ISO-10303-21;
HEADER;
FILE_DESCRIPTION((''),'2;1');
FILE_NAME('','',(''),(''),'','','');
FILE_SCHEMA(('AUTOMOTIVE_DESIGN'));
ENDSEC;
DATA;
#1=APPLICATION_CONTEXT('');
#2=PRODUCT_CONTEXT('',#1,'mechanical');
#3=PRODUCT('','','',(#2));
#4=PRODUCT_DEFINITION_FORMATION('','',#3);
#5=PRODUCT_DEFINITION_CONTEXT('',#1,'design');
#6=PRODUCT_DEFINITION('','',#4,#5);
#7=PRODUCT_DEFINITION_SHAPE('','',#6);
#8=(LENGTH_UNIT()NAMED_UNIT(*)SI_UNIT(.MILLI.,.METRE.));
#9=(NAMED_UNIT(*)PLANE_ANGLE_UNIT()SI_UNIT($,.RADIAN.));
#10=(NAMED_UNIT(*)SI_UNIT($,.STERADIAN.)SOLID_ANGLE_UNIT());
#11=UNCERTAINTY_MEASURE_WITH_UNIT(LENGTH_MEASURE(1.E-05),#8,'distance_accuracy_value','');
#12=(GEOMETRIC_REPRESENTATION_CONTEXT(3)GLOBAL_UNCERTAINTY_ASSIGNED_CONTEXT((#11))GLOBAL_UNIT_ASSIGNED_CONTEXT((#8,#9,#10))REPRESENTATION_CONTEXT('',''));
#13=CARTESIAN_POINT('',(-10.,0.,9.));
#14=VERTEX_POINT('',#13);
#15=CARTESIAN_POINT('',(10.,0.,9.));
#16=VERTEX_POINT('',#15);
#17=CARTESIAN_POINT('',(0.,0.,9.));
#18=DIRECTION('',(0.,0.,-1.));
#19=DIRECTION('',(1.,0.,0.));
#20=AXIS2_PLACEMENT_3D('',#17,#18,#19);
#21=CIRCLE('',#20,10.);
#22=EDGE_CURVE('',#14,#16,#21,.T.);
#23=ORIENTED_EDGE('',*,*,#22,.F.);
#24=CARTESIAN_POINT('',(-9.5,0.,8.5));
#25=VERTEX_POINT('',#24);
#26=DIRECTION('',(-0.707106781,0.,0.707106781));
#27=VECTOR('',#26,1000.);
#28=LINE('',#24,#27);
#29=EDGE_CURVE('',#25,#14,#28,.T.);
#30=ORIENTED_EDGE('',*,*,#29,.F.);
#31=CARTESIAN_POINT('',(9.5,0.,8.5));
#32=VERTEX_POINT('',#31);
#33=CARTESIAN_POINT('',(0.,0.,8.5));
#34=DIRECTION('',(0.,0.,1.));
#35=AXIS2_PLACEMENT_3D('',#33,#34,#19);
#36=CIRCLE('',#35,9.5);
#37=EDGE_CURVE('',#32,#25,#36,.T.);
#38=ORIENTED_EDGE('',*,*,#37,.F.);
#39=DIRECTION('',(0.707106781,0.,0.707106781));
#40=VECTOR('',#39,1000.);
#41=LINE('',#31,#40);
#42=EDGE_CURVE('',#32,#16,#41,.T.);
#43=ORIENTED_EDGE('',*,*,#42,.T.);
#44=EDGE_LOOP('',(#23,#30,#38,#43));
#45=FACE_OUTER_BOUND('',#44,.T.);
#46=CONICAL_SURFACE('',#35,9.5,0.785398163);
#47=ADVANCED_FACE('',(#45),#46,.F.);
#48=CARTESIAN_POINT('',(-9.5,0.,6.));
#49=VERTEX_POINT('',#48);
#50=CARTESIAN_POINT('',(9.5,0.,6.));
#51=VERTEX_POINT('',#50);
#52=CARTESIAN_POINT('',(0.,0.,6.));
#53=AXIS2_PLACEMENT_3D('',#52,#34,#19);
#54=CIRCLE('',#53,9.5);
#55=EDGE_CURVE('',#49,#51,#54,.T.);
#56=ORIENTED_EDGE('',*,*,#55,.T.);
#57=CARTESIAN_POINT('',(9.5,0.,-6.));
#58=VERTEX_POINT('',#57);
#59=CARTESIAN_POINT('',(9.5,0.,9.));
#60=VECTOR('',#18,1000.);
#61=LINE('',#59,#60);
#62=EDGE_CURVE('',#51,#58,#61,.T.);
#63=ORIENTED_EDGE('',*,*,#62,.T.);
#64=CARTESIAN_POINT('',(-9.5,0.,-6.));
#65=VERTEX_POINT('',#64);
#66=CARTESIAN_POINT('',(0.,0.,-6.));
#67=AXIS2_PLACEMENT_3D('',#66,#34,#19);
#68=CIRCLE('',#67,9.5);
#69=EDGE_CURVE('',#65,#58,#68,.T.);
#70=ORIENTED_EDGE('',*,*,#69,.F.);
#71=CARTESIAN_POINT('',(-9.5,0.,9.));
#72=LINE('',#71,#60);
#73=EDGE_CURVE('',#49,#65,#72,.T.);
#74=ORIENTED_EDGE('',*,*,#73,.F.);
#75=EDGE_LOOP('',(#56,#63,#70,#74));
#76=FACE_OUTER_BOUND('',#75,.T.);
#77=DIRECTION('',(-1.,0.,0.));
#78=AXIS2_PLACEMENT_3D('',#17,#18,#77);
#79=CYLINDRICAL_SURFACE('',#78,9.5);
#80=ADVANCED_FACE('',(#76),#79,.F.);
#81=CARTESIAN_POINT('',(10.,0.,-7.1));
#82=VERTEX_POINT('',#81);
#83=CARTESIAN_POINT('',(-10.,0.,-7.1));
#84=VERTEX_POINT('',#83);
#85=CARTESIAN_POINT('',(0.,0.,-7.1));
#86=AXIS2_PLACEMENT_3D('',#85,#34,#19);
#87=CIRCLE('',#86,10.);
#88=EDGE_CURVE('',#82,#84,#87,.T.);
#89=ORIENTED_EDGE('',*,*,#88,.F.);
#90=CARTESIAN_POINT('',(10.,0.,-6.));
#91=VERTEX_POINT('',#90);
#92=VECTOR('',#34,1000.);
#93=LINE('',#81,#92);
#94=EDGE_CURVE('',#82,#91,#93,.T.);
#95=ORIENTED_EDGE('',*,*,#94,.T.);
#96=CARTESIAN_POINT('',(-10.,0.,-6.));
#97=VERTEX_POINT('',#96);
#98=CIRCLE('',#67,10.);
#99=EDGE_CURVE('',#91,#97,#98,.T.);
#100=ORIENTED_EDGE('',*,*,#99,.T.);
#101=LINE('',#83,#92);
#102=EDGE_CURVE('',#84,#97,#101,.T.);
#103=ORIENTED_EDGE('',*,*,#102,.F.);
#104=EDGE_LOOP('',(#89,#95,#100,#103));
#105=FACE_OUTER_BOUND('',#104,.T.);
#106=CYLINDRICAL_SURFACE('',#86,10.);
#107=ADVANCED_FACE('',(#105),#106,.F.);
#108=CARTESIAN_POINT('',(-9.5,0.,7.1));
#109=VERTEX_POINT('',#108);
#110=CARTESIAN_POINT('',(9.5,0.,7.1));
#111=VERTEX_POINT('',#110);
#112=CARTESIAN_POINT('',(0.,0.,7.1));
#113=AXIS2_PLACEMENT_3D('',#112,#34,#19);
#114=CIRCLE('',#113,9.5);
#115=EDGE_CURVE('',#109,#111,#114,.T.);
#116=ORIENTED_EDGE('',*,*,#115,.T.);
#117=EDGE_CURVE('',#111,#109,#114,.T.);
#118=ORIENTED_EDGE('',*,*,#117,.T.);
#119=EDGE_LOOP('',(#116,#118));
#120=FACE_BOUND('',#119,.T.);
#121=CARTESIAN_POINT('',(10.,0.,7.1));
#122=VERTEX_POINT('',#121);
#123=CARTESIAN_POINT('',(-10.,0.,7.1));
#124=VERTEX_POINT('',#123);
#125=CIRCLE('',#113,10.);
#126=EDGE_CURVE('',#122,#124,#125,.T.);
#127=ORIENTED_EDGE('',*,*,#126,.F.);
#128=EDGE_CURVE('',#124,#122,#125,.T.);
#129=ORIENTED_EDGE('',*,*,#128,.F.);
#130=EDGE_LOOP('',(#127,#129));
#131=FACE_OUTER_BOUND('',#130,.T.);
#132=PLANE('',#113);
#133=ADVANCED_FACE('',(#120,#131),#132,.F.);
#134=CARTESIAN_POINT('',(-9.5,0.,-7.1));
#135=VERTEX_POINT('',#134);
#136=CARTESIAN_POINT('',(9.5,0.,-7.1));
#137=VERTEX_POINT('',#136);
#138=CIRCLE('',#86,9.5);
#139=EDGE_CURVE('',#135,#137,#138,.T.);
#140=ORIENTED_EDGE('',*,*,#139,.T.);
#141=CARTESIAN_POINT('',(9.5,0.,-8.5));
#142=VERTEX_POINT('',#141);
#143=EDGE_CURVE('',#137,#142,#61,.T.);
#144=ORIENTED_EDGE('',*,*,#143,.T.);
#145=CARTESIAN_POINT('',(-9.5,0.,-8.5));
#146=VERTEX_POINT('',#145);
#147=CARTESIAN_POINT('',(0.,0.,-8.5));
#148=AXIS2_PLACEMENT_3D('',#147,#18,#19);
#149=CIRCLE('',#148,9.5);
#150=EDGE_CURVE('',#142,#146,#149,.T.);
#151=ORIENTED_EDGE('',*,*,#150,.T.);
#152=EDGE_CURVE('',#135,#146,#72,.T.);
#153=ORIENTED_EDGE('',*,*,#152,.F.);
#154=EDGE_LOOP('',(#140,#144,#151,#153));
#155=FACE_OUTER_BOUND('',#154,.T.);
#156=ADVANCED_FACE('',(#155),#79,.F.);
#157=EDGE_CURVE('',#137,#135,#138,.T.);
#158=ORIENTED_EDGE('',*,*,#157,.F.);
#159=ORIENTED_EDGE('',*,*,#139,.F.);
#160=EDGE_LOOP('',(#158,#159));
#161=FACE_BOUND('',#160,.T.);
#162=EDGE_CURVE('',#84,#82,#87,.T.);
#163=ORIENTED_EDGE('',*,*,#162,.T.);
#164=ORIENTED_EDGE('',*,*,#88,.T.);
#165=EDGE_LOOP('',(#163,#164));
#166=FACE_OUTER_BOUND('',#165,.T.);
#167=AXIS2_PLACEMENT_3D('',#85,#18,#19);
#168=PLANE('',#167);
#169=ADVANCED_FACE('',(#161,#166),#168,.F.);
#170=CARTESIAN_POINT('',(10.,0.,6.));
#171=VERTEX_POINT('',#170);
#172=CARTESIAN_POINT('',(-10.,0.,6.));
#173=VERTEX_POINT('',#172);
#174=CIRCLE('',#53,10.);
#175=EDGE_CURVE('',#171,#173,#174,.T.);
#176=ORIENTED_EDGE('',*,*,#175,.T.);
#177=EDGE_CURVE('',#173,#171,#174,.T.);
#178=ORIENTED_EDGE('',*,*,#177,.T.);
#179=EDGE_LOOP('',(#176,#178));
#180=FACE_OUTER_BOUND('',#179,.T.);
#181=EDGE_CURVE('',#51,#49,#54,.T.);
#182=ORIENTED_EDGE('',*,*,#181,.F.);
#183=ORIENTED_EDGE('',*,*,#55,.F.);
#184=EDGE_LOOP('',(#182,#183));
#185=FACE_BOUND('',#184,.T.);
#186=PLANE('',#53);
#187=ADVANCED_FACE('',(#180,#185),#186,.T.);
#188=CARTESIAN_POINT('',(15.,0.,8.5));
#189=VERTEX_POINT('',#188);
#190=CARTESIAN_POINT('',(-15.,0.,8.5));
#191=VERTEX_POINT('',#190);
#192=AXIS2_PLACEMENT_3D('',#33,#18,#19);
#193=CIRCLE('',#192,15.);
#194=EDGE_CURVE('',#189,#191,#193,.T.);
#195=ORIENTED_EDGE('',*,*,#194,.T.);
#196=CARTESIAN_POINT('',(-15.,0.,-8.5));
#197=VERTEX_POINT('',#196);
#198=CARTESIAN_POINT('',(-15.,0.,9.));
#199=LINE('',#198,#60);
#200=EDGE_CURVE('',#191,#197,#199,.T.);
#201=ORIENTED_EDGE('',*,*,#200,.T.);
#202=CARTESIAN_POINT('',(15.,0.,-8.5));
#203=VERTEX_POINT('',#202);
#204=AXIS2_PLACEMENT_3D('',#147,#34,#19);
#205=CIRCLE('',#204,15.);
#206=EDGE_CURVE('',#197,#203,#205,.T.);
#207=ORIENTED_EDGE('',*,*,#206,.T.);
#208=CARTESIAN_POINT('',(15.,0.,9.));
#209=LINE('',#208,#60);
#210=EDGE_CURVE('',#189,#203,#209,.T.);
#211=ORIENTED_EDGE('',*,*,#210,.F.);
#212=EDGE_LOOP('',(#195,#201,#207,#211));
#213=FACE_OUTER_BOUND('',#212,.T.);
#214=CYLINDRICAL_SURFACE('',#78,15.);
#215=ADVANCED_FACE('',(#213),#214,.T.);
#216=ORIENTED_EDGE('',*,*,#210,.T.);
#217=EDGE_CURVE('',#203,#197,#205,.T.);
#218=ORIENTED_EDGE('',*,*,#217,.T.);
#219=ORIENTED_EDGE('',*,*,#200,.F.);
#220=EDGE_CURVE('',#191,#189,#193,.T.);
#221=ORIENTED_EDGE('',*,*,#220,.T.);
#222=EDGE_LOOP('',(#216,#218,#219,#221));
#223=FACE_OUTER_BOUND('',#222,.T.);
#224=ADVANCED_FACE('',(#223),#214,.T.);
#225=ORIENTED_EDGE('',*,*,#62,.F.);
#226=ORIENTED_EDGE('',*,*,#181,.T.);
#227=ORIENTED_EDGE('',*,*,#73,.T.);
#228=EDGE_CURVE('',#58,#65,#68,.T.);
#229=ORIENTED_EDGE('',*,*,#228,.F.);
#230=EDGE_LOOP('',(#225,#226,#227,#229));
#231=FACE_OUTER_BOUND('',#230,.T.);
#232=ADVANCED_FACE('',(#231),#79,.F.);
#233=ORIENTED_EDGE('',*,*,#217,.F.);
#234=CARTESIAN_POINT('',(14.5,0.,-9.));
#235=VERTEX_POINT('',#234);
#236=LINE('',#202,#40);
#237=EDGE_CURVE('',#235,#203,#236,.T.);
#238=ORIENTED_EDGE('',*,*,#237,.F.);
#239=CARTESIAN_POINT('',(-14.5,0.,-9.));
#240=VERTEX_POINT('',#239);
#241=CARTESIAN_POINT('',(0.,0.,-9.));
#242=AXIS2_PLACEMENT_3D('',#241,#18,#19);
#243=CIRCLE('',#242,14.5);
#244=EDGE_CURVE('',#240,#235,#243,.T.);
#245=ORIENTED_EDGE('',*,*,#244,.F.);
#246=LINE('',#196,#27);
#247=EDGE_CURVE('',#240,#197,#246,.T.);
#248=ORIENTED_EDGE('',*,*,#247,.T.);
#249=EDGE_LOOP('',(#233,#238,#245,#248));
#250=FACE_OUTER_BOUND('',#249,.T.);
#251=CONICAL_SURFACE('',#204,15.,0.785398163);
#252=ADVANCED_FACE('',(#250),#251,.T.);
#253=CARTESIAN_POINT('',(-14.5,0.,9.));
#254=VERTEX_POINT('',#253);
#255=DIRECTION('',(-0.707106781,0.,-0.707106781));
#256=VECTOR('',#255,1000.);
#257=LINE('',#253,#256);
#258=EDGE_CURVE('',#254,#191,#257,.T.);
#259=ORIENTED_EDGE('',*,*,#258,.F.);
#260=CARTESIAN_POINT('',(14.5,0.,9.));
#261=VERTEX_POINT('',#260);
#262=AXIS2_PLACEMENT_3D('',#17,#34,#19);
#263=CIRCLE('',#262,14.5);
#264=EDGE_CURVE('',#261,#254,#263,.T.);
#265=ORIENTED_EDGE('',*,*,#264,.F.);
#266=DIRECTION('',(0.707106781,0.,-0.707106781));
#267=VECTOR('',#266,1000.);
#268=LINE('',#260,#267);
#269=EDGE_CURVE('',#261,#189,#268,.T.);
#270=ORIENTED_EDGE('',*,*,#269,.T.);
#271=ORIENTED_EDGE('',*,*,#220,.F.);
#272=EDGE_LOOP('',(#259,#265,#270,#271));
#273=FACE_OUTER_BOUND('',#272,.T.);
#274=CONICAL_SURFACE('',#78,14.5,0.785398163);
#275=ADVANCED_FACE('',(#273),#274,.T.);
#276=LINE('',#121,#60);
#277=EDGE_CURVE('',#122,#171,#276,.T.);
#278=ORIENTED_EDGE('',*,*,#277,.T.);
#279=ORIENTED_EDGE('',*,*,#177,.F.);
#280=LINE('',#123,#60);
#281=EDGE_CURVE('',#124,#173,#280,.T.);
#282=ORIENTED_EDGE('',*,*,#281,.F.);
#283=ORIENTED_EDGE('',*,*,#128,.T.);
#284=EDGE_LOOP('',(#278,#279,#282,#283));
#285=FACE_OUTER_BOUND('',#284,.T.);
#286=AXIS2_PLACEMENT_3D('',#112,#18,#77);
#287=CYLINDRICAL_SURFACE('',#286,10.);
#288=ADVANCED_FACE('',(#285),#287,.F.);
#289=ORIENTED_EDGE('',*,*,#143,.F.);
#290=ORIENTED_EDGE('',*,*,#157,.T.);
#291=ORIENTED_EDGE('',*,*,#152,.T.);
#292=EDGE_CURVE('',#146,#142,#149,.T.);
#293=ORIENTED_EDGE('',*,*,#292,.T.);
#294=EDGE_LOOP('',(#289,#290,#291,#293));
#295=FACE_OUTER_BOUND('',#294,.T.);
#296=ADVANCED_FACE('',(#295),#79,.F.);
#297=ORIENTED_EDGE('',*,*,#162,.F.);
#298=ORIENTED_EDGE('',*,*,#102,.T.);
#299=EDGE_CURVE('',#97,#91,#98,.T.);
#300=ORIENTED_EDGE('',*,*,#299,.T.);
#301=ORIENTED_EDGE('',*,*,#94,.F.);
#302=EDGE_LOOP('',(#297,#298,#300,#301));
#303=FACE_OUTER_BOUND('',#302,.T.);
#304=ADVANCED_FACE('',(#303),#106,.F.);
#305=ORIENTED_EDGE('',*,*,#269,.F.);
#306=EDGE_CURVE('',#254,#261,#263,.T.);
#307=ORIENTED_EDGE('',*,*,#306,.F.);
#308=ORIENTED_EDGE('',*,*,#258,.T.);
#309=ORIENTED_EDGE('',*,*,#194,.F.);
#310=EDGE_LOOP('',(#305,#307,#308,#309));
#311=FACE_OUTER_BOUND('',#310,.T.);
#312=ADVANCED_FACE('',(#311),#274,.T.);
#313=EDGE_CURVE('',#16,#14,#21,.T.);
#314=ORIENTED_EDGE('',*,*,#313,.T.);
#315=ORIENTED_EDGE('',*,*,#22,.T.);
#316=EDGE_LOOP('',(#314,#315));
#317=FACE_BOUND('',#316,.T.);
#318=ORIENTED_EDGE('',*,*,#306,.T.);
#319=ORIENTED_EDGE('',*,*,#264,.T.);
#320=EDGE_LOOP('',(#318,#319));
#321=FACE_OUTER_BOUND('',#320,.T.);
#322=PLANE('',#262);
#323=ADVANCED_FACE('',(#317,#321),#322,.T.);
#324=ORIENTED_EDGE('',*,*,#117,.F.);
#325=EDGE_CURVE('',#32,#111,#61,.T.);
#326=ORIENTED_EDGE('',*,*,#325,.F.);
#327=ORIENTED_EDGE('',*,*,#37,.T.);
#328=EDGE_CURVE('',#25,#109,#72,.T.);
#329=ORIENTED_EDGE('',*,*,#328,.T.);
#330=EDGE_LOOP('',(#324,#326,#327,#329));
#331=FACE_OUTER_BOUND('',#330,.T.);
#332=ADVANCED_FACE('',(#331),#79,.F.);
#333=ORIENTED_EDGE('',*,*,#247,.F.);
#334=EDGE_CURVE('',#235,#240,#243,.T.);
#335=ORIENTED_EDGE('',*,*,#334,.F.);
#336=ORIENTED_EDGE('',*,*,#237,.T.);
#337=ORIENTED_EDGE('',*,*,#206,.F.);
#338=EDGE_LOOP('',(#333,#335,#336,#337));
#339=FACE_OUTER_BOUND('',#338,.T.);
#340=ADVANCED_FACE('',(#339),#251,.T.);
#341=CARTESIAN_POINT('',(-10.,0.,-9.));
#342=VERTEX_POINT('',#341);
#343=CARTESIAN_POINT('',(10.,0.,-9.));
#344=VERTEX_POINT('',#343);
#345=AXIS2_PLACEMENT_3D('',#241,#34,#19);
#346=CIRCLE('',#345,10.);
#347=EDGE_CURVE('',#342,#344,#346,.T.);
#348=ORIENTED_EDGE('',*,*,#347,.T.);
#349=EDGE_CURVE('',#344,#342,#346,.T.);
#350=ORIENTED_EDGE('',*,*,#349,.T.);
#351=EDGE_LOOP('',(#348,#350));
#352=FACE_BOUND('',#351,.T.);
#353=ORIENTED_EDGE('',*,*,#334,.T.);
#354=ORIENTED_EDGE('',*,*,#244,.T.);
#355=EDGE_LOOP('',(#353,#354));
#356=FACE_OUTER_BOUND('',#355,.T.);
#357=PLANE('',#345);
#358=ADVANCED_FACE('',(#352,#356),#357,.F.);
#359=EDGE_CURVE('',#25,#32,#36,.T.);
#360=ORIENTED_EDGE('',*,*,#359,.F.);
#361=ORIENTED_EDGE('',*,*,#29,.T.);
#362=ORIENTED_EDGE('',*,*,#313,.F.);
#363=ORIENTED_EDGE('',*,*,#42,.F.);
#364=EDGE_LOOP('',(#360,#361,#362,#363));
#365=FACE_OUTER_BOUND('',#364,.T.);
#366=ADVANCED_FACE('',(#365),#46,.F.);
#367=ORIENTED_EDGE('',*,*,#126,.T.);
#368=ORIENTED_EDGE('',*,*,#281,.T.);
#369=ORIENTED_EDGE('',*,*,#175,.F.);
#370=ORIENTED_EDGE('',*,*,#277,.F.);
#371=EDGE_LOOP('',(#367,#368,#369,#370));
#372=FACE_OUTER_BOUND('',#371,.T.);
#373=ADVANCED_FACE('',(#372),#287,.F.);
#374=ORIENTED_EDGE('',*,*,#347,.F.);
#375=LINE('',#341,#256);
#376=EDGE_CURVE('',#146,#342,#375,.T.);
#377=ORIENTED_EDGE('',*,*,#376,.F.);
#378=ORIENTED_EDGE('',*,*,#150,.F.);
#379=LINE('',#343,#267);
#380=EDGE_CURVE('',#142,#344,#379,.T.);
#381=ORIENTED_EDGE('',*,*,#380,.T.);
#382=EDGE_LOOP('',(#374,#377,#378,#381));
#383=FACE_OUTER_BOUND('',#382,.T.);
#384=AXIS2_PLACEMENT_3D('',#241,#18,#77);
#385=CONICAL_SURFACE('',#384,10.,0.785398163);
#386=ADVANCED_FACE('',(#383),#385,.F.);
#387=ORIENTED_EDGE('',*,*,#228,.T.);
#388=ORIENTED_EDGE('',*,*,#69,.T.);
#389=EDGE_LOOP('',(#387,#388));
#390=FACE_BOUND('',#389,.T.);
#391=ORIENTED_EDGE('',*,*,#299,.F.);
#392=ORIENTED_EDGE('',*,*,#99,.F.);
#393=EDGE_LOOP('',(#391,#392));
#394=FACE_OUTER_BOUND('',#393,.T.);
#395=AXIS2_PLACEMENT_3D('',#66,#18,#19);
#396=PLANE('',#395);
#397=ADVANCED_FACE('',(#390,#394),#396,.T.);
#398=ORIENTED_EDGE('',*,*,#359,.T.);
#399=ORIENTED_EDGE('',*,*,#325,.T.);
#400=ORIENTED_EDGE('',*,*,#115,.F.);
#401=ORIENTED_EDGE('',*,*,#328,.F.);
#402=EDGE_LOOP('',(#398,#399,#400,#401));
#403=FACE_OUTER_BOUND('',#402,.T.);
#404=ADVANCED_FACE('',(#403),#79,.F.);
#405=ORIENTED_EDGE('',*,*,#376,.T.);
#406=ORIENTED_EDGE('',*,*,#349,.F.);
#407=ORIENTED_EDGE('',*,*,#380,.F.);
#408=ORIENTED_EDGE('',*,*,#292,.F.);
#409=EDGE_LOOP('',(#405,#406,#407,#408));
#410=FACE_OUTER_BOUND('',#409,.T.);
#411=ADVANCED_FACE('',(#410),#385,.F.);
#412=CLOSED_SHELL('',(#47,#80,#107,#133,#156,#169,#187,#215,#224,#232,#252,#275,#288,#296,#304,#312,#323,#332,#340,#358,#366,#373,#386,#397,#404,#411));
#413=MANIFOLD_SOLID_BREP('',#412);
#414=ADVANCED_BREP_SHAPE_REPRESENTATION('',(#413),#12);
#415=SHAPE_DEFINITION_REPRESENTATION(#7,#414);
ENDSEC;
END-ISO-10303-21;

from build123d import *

# Parameters (mm, degrees)
SKETCH1_R           = 15
SKETCH1_R_2         = 9.5
BOSS_EXTRUDE1_DEPTH = 9
CUT_EXTRUDE1_START  = 6
SKETCH2_R           = 10
SKETCH2_R_2         = 9.5
CUT_EXTRUDE1_DEPTH  = 1.1
CHAMFER1_SIZE       = 0.5


with BuildPart() as part:
    # Sketch1 → Boss-Extrude1 (new, symmetric)
    with BuildSketch(Plane.XY):
        Circle(SKETCH1_R)
        Circle(SKETCH1_R_2, mode=Mode.SUBTRACT)
    extrude(amount=BOSS_EXTRUDE1_DEPTH, both=True)

    # Sketch2 → Cut-Extrude1 (cut)
    with BuildSketch(Plane.XY.offset(CUT_EXTRUDE1_START)):
        Circle(SKETCH2_R)
        Circle(SKETCH2_R_2, mode=Mode.SUBTRACT)
    cut_extrude1 = extrude(amount=CUT_EXTRUDE1_DEPTH, mode=Mode.SUBTRACT)

    # Mirror1: Cut-Extrude1 across plane
    add(cut_extrude1.mirror(Plane.XY), mode=Mode.SUBTRACT)

    # Chamfer1
    chamfer1_edges = [part.edges().sort_by_distance(p)[0] for p in [
        (-15, 0, -9),
        (-15, 0, 9),
        (-9.5, 0, -9),
        (-9.5, 0, 9),
    ]]
    chamfer(chamfer1_edges, length=CHAMFER1_SIZE)


solid = part.part
